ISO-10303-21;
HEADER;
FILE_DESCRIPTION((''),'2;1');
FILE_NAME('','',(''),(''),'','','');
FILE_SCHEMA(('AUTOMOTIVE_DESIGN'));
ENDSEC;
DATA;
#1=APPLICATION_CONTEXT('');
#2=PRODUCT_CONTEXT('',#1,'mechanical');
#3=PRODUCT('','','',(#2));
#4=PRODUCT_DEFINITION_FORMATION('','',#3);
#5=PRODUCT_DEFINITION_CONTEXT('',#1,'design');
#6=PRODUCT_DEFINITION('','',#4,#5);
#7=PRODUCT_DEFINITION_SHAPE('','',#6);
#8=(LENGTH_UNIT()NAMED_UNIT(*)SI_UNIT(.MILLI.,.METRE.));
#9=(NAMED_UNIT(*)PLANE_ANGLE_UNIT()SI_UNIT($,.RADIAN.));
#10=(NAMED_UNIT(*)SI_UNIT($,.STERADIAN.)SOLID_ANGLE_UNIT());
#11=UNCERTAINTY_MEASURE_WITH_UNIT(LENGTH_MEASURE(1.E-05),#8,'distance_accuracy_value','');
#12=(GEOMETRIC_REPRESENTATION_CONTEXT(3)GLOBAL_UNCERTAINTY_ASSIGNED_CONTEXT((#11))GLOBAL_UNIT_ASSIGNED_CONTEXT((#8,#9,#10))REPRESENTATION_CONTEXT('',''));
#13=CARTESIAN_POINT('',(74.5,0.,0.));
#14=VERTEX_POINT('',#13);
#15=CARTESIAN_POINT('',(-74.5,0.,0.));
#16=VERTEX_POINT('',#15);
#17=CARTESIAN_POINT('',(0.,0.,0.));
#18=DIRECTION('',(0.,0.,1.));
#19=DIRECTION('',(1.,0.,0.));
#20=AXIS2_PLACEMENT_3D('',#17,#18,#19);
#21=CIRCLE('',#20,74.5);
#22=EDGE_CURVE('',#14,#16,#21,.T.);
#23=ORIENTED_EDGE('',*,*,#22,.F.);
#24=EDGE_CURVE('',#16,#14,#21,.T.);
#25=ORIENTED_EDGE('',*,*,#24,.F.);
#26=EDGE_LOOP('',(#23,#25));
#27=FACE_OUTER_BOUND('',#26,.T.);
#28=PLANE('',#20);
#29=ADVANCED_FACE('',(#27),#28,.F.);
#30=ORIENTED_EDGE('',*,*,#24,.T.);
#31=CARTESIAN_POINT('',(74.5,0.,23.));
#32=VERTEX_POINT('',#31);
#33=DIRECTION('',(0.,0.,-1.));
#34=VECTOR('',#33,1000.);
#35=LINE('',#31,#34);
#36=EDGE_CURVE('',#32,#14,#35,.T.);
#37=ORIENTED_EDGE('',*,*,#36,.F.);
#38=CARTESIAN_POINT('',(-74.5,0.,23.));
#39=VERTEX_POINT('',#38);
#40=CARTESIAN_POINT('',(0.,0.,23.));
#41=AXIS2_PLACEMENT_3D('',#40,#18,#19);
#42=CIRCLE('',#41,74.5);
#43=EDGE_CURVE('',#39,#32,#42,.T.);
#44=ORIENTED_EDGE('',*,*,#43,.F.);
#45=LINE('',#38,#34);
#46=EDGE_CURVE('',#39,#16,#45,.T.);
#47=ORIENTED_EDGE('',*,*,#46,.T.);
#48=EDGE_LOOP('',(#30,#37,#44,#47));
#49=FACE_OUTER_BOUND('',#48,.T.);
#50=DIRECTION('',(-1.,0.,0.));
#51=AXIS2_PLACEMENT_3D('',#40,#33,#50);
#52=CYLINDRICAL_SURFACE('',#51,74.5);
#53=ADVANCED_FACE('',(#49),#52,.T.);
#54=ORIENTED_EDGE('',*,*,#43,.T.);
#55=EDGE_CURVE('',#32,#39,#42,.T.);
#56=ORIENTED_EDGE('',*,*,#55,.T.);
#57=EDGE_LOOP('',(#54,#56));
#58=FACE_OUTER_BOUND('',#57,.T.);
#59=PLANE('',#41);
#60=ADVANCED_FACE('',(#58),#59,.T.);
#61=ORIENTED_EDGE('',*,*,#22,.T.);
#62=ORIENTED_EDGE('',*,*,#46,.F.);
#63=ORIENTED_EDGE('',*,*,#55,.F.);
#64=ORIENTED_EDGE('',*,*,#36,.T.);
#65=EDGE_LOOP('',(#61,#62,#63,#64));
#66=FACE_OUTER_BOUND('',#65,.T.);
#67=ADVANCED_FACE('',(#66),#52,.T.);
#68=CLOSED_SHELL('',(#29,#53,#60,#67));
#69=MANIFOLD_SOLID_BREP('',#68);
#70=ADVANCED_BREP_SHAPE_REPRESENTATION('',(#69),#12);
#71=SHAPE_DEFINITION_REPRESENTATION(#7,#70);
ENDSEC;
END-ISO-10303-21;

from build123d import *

# Parameters (mm, degrees)
SKETCH2_R           = 74.5
BOSS_EXTRUDE1_DEPTH = 23


with BuildPart() as part:
    # Sketch2 → Boss-Extrude1 (new body)
    with BuildSketch(Plane.XY):
        Circle(SKETCH2_R)
    extrude(amount=BOSS_EXTRUDE1_DEPTH)


solid = part.part
